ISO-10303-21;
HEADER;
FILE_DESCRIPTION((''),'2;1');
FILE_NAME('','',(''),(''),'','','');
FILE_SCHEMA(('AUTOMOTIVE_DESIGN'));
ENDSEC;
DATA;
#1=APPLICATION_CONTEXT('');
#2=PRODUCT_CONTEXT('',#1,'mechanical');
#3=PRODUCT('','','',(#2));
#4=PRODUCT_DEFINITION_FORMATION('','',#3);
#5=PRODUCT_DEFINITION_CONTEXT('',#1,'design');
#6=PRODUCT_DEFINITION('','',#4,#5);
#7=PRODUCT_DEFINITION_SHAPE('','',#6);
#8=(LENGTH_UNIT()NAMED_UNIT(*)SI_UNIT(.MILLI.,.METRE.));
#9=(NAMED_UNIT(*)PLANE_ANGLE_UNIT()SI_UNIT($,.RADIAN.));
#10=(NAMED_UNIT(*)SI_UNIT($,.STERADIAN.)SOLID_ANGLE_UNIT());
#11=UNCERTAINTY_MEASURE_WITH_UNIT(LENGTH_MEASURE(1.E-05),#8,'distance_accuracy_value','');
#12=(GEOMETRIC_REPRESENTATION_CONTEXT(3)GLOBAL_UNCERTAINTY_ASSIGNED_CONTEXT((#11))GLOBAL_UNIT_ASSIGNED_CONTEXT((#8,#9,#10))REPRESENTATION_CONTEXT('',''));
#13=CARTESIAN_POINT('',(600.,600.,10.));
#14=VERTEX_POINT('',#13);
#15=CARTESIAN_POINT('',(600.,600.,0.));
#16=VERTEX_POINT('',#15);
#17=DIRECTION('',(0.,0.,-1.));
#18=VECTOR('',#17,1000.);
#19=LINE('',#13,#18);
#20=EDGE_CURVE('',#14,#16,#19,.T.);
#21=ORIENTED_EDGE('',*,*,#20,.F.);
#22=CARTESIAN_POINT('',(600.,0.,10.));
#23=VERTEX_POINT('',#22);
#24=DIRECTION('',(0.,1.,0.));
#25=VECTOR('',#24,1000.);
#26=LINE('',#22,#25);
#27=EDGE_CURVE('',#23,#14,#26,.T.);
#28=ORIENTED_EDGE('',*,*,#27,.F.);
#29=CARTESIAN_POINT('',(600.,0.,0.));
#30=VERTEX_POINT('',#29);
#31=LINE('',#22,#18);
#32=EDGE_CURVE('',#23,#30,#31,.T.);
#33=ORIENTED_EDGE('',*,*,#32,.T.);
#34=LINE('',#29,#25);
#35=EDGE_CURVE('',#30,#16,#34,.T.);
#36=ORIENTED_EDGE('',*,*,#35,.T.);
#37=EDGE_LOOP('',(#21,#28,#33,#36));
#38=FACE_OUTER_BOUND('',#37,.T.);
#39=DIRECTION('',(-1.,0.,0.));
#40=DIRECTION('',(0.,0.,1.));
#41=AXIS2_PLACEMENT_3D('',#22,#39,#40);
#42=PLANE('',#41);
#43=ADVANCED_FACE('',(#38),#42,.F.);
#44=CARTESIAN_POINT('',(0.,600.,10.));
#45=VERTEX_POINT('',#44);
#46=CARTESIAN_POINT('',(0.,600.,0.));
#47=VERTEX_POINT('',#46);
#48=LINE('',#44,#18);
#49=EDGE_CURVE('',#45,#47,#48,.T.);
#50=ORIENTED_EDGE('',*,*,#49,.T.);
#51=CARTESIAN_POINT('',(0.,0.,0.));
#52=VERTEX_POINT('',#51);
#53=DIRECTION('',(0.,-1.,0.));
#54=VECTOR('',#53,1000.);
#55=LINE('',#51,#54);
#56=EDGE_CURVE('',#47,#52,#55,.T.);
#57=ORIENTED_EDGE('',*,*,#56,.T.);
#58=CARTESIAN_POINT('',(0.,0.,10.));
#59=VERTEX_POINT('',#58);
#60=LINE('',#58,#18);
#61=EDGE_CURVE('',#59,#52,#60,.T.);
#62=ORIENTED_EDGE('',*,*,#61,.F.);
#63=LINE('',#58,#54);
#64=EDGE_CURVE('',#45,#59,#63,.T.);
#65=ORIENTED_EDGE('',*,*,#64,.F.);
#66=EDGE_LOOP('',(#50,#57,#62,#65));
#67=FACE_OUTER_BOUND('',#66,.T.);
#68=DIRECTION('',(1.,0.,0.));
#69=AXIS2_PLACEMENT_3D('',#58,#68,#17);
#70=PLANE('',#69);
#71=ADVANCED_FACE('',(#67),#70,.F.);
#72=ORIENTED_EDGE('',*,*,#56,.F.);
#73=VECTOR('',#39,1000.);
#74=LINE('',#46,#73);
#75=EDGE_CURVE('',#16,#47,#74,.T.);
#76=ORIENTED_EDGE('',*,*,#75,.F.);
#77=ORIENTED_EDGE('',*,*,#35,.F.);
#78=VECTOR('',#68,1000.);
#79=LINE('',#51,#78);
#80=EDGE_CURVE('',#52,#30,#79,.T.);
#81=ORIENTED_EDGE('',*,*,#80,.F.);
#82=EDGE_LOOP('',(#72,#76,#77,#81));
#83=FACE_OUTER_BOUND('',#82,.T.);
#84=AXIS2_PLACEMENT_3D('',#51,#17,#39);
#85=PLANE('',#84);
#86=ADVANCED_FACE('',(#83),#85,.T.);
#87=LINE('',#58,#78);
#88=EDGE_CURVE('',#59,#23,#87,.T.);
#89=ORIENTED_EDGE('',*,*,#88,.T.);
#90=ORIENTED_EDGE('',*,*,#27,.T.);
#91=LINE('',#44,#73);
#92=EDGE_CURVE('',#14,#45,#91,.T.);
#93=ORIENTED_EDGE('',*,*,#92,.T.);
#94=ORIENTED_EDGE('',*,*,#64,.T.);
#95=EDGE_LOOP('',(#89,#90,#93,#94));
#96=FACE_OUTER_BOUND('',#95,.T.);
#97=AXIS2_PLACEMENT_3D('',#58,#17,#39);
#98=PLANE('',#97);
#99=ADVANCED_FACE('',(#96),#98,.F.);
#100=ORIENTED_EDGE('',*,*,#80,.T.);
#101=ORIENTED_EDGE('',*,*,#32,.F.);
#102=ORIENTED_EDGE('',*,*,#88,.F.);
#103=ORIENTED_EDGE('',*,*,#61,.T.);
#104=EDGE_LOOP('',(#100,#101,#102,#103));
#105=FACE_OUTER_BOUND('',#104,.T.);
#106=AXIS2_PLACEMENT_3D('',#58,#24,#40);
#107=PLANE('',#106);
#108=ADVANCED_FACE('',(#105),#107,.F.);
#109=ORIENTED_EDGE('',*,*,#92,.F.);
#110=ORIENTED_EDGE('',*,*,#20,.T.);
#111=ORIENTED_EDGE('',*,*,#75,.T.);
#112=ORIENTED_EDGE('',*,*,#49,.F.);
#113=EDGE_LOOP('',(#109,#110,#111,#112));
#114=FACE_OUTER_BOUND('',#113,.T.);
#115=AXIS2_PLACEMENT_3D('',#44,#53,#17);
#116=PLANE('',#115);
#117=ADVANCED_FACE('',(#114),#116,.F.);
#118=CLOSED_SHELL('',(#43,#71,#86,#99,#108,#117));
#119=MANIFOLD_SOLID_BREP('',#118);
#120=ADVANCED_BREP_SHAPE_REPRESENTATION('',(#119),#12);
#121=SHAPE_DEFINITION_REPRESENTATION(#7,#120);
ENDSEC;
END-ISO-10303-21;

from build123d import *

# Parameters (mm, degrees)
SKETCH1_W           = 600
SKETCH1_H           = 600
BOSS_EXTRUDE1_DEPTH = 10


with BuildPart() as part:
    # Sketch1 → Boss-Extrude1 (new body)
    with BuildSketch(Plane.XY):
        with Locations((300, 300)):
            Rectangle(SKETCH1_W, SKETCH1_H)
    extrude(amount=BOSS_EXTRUDE1_DEPTH)


solid = part.part
